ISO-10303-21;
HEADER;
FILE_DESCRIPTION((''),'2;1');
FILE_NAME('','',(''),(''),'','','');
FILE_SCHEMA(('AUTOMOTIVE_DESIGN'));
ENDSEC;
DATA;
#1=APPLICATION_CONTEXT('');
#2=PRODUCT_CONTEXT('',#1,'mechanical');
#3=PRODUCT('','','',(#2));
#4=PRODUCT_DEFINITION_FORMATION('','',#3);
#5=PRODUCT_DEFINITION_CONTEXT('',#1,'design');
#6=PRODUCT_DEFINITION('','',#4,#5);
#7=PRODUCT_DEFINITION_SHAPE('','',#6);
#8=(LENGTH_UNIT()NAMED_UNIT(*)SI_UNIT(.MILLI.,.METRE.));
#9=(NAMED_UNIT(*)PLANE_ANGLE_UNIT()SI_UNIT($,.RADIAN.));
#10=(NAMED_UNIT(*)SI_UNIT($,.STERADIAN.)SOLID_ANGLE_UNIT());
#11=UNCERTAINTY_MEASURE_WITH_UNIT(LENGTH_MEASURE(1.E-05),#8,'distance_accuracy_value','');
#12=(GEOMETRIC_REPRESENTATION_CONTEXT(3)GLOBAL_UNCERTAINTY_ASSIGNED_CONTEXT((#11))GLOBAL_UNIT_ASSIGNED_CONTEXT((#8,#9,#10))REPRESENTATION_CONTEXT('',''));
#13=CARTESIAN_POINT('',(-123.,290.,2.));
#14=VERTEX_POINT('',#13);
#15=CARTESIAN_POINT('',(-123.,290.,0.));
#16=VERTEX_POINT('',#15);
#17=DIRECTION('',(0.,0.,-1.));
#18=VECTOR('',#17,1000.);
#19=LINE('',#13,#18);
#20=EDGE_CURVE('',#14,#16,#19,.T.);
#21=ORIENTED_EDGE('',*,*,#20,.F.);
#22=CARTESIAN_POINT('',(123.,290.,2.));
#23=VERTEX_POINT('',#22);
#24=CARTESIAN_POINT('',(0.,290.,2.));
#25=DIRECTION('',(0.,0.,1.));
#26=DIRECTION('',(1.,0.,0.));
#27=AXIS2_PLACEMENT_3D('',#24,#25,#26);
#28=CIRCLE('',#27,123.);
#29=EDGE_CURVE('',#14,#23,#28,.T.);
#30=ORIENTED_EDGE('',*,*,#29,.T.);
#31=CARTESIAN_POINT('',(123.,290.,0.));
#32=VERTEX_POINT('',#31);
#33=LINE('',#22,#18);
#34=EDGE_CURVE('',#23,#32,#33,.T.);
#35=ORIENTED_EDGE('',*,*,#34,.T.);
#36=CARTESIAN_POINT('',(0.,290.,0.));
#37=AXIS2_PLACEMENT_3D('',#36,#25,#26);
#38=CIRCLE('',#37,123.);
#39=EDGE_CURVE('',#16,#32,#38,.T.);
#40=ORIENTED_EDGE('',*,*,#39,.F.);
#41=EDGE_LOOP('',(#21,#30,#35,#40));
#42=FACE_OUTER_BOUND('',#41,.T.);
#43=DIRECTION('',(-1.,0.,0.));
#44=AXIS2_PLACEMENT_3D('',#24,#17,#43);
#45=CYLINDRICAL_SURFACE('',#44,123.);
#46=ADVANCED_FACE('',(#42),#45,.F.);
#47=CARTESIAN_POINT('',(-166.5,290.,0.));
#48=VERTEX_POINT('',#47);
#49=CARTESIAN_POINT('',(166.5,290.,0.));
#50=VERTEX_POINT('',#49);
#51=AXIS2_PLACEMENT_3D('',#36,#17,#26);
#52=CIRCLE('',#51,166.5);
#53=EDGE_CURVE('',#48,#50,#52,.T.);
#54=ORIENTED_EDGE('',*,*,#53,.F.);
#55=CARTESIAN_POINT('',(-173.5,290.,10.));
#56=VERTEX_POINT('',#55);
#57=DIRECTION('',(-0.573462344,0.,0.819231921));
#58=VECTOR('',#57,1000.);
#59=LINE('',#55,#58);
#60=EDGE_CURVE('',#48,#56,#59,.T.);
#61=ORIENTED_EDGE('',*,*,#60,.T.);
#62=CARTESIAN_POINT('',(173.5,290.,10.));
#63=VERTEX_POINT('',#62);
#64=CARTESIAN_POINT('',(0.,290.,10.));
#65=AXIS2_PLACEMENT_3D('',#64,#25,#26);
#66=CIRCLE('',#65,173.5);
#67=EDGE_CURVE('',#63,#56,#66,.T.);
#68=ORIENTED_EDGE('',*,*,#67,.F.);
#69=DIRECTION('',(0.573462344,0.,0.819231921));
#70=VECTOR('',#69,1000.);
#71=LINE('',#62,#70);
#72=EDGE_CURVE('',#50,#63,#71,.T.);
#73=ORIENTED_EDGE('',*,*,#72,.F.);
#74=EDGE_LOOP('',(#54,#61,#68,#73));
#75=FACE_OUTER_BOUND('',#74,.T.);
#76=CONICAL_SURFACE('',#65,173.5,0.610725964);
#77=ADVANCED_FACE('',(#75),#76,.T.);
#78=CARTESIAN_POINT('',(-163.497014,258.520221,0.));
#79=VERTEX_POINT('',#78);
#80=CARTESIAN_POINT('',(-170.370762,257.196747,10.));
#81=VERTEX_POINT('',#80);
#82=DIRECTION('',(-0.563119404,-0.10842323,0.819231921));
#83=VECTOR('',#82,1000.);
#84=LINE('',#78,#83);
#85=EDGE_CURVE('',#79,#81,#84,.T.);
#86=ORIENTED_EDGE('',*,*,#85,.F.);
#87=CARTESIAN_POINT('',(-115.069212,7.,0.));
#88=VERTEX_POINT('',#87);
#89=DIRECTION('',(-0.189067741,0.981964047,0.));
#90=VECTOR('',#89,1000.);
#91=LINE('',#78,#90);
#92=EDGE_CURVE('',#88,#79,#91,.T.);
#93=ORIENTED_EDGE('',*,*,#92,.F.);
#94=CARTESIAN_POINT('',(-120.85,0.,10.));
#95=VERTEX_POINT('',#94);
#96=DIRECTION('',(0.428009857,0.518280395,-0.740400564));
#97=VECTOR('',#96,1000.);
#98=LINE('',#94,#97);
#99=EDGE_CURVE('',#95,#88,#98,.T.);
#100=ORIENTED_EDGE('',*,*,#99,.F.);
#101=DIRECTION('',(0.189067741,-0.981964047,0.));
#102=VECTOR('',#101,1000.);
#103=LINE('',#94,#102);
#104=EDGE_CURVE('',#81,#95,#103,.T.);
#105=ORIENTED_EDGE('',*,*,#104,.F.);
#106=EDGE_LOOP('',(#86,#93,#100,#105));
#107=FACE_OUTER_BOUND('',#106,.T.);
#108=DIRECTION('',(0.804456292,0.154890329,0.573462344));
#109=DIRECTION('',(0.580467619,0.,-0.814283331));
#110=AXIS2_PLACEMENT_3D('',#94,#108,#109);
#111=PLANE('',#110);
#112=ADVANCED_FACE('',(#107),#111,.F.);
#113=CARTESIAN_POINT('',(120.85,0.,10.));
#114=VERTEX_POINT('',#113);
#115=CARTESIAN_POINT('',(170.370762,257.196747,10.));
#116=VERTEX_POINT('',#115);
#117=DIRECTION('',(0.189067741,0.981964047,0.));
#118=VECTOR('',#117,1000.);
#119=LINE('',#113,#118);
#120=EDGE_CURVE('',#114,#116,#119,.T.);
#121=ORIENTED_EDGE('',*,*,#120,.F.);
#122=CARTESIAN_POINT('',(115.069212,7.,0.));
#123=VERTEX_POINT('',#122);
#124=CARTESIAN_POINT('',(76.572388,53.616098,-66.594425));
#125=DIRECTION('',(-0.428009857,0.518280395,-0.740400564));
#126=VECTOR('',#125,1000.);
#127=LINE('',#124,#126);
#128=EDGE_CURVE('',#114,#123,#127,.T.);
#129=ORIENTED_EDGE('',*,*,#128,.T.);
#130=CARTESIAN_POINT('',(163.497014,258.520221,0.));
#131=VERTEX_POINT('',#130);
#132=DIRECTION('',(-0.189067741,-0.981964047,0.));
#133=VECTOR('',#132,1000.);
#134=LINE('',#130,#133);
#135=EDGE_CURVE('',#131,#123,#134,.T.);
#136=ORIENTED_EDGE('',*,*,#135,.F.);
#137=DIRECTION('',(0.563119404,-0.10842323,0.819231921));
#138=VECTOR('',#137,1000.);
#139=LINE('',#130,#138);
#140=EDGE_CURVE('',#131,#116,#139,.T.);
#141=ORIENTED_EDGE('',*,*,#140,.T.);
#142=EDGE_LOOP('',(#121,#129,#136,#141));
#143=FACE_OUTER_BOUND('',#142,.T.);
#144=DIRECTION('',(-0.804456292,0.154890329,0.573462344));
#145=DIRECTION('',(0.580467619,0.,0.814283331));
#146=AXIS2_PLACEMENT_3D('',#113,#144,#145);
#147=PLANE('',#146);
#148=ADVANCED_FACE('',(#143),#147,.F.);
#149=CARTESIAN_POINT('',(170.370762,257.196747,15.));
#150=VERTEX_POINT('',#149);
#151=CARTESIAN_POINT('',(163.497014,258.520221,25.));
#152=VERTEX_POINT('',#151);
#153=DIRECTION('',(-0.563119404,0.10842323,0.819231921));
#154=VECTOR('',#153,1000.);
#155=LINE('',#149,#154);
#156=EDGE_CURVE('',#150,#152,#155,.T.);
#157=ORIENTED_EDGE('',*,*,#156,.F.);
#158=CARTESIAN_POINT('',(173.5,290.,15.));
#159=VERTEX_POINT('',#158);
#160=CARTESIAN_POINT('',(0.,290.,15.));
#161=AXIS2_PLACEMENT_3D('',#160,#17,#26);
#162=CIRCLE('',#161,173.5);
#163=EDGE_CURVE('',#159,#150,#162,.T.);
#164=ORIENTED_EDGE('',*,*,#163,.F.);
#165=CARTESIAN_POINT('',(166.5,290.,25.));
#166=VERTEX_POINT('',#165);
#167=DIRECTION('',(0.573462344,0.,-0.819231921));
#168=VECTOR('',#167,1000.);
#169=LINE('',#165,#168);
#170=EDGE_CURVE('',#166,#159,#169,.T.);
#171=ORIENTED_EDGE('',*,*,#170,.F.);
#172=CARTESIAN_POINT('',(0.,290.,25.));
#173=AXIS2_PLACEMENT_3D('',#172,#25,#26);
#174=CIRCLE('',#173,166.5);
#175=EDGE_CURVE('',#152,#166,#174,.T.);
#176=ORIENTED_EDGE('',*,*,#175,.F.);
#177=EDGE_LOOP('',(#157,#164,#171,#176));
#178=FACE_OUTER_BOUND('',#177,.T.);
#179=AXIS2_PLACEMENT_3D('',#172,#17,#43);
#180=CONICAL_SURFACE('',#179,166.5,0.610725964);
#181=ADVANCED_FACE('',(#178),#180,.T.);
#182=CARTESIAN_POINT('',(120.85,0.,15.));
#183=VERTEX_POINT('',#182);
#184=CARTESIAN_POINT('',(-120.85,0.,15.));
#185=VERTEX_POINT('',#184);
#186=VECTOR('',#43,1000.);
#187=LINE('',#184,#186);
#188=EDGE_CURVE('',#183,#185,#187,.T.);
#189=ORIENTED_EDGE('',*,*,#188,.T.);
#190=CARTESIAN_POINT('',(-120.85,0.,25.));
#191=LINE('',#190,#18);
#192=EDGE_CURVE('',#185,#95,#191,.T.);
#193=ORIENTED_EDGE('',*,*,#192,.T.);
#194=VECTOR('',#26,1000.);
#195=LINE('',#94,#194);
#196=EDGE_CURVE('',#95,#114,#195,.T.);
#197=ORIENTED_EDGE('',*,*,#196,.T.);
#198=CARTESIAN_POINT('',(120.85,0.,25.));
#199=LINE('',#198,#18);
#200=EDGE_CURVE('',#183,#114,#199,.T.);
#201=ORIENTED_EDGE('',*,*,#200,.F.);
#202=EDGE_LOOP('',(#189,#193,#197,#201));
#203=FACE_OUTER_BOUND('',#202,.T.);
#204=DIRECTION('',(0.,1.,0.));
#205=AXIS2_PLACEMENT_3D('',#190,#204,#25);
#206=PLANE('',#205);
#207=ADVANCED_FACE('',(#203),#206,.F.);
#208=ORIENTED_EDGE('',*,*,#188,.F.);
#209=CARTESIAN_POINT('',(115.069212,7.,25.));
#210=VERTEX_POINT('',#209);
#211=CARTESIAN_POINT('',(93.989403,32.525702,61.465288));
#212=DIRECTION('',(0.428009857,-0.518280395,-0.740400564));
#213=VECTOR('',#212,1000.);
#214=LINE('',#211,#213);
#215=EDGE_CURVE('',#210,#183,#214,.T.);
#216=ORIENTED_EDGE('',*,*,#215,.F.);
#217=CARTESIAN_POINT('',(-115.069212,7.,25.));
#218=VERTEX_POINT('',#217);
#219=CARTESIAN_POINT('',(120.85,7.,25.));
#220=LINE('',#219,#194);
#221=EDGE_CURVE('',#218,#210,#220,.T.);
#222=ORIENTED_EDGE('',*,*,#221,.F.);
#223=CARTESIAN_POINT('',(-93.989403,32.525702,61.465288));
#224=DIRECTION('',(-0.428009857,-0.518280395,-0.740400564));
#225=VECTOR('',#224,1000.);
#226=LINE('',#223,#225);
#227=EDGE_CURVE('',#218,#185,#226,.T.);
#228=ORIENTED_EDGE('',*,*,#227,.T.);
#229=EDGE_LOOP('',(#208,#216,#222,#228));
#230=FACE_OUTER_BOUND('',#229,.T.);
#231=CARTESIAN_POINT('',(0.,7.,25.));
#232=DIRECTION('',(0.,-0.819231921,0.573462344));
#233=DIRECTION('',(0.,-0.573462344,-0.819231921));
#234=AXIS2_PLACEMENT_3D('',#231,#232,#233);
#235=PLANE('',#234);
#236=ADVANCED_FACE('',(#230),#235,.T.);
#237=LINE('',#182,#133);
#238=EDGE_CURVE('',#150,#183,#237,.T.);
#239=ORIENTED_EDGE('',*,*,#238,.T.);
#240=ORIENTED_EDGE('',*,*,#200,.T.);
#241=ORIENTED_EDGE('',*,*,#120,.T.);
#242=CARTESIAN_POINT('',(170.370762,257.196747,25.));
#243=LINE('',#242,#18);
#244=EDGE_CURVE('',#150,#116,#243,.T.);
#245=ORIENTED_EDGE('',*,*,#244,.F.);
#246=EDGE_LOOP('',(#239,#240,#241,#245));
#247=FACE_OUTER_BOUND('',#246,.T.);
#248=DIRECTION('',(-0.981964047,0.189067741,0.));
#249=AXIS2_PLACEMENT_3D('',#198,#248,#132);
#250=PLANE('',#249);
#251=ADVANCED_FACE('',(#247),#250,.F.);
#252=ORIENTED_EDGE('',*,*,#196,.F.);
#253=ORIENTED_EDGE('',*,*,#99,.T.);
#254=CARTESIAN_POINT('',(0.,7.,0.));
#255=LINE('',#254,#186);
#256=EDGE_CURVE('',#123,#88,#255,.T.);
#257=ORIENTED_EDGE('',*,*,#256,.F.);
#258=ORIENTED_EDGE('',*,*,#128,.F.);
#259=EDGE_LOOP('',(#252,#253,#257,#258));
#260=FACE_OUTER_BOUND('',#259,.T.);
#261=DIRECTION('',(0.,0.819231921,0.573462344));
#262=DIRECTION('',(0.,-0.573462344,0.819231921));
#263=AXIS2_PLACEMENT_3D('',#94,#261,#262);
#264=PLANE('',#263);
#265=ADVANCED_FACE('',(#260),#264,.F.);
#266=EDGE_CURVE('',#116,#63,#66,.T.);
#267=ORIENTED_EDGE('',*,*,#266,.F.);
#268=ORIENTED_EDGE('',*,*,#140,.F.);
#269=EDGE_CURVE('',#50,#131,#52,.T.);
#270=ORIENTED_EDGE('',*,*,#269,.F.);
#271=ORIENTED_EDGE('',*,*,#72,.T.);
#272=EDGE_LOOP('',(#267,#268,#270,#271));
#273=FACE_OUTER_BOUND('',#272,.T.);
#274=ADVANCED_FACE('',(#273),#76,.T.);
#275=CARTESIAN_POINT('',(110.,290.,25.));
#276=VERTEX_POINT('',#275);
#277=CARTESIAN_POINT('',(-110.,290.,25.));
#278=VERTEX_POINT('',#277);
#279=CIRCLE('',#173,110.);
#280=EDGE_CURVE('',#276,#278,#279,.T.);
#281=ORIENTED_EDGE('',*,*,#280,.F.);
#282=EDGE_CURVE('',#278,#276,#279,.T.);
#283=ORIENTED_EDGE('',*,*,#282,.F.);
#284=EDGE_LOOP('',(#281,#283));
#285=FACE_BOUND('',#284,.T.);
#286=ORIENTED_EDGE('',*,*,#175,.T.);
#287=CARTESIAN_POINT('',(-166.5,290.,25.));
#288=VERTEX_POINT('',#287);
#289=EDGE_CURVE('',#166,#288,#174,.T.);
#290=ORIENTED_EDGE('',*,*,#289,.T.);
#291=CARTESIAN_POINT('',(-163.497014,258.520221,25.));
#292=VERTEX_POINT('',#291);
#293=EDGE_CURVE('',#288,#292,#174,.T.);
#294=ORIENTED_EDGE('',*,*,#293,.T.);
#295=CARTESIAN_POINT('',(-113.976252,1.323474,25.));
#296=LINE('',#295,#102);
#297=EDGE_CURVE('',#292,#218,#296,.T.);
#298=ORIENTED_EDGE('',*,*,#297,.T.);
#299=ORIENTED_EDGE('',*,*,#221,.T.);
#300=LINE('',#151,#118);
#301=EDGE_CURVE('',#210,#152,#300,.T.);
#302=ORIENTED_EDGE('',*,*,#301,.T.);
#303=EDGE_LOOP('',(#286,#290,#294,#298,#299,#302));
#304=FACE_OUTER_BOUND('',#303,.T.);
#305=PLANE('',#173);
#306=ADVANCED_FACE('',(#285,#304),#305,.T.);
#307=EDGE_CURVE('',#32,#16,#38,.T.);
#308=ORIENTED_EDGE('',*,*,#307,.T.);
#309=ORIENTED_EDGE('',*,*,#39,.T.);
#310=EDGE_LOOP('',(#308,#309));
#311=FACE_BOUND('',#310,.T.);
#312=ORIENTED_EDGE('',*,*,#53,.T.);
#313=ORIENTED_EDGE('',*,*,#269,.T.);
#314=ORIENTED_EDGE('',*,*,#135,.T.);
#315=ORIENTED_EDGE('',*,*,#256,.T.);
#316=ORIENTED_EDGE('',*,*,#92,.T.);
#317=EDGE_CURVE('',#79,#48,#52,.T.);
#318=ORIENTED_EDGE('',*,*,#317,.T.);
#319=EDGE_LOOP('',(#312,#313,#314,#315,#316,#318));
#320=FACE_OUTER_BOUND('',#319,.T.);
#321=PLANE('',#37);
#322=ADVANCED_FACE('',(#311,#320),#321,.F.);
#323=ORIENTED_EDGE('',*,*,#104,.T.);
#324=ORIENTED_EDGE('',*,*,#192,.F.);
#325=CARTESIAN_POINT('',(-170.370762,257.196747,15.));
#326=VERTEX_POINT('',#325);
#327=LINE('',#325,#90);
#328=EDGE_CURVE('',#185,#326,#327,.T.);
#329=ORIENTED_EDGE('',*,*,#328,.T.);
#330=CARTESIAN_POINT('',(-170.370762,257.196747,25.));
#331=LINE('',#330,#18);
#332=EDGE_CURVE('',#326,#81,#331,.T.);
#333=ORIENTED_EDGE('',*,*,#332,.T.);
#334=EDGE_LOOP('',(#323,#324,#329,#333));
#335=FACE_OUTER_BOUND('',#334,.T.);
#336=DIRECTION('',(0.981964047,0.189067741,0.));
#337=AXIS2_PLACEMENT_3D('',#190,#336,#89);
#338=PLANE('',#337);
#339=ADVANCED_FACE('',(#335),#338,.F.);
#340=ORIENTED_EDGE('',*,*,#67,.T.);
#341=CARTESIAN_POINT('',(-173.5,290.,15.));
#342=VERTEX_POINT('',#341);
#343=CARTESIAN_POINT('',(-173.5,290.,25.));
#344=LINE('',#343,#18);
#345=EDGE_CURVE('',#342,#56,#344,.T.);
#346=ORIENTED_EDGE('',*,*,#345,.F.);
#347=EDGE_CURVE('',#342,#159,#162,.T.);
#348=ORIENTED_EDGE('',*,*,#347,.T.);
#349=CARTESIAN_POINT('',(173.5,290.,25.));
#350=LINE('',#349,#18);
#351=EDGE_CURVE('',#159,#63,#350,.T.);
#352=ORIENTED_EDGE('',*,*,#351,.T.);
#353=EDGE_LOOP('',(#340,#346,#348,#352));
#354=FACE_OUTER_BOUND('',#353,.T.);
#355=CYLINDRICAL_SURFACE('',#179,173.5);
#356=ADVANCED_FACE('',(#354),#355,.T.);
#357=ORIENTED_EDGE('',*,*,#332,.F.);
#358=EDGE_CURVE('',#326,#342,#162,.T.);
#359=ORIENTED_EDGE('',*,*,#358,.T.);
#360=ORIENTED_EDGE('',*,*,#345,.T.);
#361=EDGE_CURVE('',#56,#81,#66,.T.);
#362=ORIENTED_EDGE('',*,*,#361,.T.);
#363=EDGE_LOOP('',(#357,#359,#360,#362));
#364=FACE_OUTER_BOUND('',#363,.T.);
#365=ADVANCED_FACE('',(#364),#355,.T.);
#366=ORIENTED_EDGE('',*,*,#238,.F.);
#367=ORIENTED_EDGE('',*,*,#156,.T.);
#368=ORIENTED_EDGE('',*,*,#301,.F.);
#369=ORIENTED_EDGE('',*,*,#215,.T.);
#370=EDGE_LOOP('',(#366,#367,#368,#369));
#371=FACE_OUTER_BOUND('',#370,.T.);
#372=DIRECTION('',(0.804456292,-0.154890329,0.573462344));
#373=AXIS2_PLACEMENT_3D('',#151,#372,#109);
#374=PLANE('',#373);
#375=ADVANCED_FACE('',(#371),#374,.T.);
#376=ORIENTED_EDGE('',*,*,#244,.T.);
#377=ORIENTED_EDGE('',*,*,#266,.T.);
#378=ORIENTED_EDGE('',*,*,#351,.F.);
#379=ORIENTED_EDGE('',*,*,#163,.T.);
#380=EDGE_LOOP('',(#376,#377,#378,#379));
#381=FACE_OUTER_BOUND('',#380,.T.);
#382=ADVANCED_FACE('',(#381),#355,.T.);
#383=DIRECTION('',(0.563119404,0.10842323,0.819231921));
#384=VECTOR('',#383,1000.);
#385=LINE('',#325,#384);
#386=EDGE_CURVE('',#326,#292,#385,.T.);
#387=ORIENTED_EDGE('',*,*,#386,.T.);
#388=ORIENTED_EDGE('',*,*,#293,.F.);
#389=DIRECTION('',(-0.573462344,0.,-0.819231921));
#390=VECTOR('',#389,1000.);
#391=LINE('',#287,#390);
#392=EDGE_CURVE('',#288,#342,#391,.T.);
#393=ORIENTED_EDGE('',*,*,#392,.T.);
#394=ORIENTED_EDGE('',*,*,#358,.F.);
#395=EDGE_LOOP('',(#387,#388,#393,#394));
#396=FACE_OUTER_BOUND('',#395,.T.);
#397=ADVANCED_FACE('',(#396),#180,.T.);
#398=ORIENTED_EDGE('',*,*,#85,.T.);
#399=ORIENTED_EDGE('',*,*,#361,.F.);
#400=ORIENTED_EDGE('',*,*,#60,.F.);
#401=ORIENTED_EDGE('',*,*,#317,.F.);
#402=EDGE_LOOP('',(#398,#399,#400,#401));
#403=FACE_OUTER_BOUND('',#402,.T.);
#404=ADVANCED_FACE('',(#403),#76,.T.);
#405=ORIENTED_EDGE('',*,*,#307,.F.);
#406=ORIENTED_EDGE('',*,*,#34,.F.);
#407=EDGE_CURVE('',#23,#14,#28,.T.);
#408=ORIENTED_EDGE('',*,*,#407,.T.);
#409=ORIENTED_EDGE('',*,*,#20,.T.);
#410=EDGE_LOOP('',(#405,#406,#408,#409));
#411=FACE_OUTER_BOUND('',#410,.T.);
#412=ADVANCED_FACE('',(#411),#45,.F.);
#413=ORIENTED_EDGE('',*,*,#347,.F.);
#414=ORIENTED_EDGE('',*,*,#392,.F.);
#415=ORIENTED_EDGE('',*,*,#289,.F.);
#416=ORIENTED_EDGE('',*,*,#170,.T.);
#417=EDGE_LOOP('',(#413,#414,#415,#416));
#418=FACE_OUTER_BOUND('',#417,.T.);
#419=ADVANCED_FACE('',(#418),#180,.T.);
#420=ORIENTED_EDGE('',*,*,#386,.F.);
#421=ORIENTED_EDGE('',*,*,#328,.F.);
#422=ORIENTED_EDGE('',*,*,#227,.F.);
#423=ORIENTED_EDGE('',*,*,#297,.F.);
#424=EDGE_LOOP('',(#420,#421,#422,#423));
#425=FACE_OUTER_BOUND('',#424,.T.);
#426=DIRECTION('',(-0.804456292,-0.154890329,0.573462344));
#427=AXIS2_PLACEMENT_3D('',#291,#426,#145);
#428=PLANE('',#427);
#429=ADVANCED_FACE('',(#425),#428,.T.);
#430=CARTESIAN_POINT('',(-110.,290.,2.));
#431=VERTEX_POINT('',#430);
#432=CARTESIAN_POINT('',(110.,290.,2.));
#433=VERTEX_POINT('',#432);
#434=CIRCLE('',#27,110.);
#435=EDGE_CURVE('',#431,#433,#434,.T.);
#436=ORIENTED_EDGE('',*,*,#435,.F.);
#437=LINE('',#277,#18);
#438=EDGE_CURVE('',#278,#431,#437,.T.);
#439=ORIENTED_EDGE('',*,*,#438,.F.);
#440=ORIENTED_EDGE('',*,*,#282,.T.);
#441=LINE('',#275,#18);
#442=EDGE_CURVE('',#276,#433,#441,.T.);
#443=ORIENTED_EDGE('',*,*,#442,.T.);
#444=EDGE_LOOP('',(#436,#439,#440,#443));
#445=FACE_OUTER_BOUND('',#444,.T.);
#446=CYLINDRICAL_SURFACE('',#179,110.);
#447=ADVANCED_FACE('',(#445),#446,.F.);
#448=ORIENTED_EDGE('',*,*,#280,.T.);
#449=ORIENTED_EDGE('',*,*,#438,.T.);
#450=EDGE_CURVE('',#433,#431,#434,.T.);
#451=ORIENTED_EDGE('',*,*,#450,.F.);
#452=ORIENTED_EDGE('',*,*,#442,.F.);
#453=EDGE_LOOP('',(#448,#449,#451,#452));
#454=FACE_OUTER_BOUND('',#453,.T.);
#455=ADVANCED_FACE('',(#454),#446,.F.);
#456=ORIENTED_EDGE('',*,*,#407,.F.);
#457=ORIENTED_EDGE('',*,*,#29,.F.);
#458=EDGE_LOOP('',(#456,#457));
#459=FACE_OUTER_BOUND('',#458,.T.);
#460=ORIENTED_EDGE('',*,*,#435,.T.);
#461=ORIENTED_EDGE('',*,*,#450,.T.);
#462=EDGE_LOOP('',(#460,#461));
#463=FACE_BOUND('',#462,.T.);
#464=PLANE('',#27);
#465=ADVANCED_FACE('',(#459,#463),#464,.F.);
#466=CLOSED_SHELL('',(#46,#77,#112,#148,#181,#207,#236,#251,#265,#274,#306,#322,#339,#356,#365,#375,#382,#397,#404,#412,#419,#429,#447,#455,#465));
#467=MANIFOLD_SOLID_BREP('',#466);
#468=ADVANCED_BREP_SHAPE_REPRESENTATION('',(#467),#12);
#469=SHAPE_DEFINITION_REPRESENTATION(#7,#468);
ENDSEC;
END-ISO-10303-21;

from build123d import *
from OCP.BRepFilletAPI import BRepFilletAPI_MakeChamfer

# Parameters (mm, degrees)
SKETCH1_R           = 110
BOSS_EXTRUDE1_DEPTH = 25
SKETCH2_R           = 123
SKETCH2_R_2         = 110
CUT_EXTRUDE2_DEPTH  = 2
CHAMFER1_SIZE       = 7
CHAMFER1_SIZE2      = 10
CHAMFER2_SIZE       = 10
CHAMFER2_SIZE2      = 7


with BuildPart() as part:
    # Sketch1 → Boss-Extrude1 (new body)
    with BuildSketch(Plane.XY):
        with BuildLine():
            Line((-120.85, 0), (120.85, 0))
            Line((120.85, 0), (170.370762123, 257.196746905))
            ThreePointArc((170.370762123, 257.196746905), (0, 463.5), (-170.370762123, 257.196746905))
            Line((-170.370762123, 257.196746905), (-120.85, 0))
        make_face()
        with Locations((0, 290)):
            Circle(SKETCH1_R, mode=Mode.SUBTRACT)
    extrude(amount=BOSS_EXTRUDE1_DEPTH)

    # Sketch2 → Cut-Extrude2 (cut)
    with BuildSketch(Plane.XY):
        with Locations((0, 290)):
            Circle(SKETCH2_R)
        with Locations((0, 290)):
            Circle(SKETCH2_R_2, mode=Mode.SUBTRACT)
    extrude(amount=CUT_EXTRUDE2_DEPTH, mode=Mode.SUBTRACT)

    # Chamfer1
    chamfer1_edges = [part.edges().sort_by_distance(p)[0] for p in [
        (0, 463.5, 0),
        (145.610381062, 128.598373453, 0),
        (0, 0, 0),
        (-145.610381062, 128.598373453, 0),
    ]]
    chamfer1_side = [part.faces().sort_by_distance(p)[0] for p in [
        (-139.924807111, 129.693076082, 0),
    ]]
    chamfer(chamfer1_edges, length=CHAMFER1_SIZE, length2=CHAMFER1_SIZE2, reference=chamfer1_side[0])

    # Chamfer2: one chamfer whose edges measure the first distance from different faces: ONE call of the kernel's chamfer builder (chamfer() names one face for all edges)
    chamfer2_edges_1 = [part.edges().sort_by_distance(p)[0] for p in [
        (145.610381062, 128.598373453, 25),
    ]]
    chamfer2_side_1 = [part.faces().sort_by_distance(p)[0] for p in [
        (145.610381062, 128.598373453, 17.5),
    ]]
    chamfer2_edges_2 = [part.edges().sort_by_distance(p)[0] for p in [
        (0, 463.5, 25),
    ]]
    chamfer2_side_2 = [part.faces().sort_by_distance(p)[0] for p in [
        (0, 463.5, 17.5),
    ]]
    chamfer2_edges_3 = [part.edges().sort_by_distance(p)[0] for p in [
        (-145.610381062, 128.598373453, 25),
    ]]
    chamfer2_side_3 = [part.faces().sort_by_distance(p)[0] for p in [
        (-145.610381062, 128.598373453, 17.5),
    ]]
    chamfer2_edges_4 = [part.edges().sort_by_distance(p)[0] for p in [
        (0, 0, 25),
    ]]
    chamfer2_side_4 = [part.faces().sort_by_distance(p)[0] for p in [
        (0, 0, 17.5),
    ]]
    chamfer2 = BRepFilletAPI_MakeChamfer(part.part.solid().wrapped)
    for e in chamfer2_edges_1:
        chamfer2.Add(CHAMFER2_SIZE, CHAMFER2_SIZE2, e.wrapped, chamfer2_side_1[0].wrapped)  # the first distance lies on this face
    for e in chamfer2_edges_2:
        chamfer2.Add(CHAMFER2_SIZE, CHAMFER2_SIZE2, e.wrapped, chamfer2_side_2[0].wrapped)  # the first distance lies on this face
    for e in chamfer2_edges_3:
        chamfer2.Add(CHAMFER2_SIZE, CHAMFER2_SIZE2, e.wrapped, chamfer2_side_3[0].wrapped)  # the first distance lies on this face
    for e in chamfer2_edges_4:
        chamfer2.Add(CHAMFER2_SIZE, CHAMFER2_SIZE2, e.wrapped, chamfer2_side_4[0].wrapped)  # the first distance lies on this face
    add(Compound.cast(chamfer2.Shape()), mode=Mode.REPLACE)


solid = part.part
